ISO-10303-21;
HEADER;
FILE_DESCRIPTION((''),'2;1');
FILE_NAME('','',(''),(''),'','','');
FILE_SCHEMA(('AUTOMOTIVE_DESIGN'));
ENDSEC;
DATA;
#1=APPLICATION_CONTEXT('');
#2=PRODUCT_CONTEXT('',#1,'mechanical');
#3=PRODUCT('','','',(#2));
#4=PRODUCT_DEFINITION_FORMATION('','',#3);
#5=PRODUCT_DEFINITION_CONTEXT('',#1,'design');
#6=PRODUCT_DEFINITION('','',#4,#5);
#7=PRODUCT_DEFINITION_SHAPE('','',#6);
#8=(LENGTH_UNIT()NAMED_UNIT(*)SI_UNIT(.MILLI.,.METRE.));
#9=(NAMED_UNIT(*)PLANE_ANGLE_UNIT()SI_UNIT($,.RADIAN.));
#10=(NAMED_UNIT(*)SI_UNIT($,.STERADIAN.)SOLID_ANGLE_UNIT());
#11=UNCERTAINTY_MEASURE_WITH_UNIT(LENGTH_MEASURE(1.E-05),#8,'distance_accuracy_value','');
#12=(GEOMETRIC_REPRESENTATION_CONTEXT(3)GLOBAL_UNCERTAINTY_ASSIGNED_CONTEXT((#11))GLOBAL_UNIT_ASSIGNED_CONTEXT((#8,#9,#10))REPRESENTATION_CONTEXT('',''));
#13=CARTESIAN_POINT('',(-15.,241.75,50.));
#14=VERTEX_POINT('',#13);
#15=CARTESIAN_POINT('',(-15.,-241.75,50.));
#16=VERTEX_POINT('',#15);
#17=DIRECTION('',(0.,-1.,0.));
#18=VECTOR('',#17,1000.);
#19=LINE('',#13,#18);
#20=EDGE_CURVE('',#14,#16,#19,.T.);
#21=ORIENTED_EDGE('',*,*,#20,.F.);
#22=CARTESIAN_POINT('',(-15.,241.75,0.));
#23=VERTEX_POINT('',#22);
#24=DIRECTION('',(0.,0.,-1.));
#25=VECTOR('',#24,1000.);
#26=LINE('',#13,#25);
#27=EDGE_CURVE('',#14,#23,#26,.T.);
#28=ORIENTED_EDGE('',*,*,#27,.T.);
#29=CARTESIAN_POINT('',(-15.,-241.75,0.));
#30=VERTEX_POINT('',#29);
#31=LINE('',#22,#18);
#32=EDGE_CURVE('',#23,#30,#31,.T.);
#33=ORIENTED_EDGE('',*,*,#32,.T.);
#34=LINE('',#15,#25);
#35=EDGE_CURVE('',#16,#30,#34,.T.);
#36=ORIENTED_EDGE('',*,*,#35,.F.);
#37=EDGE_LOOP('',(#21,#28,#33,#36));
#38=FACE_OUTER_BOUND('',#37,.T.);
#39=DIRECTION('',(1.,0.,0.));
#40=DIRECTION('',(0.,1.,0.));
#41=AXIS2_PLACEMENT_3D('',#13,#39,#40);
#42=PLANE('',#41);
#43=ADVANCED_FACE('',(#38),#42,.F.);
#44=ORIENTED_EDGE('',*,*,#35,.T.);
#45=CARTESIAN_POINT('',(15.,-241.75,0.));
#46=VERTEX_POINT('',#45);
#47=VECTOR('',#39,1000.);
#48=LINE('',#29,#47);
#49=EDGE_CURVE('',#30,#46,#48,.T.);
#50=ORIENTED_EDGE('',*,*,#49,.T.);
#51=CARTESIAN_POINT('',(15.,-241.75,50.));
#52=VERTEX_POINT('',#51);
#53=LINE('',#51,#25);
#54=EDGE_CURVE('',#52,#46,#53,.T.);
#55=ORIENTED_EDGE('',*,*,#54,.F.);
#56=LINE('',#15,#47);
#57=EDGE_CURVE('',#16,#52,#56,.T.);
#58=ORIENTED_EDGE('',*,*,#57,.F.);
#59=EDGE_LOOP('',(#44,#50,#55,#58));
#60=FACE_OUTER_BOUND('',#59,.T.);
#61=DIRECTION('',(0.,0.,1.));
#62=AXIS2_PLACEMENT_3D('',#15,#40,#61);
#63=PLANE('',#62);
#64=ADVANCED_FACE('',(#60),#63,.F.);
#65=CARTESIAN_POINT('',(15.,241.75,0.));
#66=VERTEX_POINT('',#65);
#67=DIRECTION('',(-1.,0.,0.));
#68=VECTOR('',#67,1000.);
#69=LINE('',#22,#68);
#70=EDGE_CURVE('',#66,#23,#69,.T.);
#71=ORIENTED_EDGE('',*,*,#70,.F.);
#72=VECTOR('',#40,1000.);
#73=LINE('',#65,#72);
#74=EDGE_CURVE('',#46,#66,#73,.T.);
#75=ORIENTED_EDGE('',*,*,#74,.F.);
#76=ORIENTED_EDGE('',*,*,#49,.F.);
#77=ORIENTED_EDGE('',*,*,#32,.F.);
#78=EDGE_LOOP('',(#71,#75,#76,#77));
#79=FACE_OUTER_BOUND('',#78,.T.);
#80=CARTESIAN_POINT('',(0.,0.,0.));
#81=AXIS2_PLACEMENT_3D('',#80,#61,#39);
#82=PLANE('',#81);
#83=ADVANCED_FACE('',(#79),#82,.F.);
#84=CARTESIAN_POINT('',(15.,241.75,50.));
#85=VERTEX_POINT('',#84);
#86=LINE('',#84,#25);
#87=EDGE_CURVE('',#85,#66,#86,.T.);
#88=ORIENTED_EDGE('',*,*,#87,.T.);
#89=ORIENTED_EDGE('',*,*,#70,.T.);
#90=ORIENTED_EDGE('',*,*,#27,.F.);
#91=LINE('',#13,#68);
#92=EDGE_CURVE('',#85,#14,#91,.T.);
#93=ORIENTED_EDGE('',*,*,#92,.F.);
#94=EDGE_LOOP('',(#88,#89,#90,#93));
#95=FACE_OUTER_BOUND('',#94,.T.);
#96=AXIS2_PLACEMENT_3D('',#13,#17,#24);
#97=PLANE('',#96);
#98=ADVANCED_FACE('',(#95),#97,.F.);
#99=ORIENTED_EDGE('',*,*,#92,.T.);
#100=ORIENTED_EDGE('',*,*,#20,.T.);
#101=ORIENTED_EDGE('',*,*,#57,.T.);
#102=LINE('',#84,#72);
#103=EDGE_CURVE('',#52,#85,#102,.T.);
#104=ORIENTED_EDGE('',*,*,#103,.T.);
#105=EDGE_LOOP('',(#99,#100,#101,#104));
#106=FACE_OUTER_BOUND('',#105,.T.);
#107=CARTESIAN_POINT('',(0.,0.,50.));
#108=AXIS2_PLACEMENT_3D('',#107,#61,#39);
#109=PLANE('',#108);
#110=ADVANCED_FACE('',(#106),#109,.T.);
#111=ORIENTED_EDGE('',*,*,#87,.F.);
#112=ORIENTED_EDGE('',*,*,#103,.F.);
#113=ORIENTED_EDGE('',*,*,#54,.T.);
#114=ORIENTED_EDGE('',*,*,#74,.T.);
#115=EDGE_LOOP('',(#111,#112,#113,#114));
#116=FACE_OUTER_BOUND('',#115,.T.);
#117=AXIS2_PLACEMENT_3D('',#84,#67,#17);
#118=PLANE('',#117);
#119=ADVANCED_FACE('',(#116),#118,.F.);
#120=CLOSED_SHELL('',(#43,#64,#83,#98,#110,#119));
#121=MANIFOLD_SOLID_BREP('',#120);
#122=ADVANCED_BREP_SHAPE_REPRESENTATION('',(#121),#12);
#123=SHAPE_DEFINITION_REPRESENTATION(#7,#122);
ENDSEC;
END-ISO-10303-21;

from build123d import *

# Parameters (mm, degrees)
SKETCH_1_W      = 30
SKETCH_1_H      = 483.5
EXTRUDE_1_DEPTH = 50


with BuildPart() as part:
    # 草图1 → 凸台-拉伸1 (new body)
    with BuildSketch(Plane.XY):
        Rectangle(SKETCH_1_W, SKETCH_1_H)
    extrude(amount=EXTRUDE_1_DEPTH)


solid = part.part
